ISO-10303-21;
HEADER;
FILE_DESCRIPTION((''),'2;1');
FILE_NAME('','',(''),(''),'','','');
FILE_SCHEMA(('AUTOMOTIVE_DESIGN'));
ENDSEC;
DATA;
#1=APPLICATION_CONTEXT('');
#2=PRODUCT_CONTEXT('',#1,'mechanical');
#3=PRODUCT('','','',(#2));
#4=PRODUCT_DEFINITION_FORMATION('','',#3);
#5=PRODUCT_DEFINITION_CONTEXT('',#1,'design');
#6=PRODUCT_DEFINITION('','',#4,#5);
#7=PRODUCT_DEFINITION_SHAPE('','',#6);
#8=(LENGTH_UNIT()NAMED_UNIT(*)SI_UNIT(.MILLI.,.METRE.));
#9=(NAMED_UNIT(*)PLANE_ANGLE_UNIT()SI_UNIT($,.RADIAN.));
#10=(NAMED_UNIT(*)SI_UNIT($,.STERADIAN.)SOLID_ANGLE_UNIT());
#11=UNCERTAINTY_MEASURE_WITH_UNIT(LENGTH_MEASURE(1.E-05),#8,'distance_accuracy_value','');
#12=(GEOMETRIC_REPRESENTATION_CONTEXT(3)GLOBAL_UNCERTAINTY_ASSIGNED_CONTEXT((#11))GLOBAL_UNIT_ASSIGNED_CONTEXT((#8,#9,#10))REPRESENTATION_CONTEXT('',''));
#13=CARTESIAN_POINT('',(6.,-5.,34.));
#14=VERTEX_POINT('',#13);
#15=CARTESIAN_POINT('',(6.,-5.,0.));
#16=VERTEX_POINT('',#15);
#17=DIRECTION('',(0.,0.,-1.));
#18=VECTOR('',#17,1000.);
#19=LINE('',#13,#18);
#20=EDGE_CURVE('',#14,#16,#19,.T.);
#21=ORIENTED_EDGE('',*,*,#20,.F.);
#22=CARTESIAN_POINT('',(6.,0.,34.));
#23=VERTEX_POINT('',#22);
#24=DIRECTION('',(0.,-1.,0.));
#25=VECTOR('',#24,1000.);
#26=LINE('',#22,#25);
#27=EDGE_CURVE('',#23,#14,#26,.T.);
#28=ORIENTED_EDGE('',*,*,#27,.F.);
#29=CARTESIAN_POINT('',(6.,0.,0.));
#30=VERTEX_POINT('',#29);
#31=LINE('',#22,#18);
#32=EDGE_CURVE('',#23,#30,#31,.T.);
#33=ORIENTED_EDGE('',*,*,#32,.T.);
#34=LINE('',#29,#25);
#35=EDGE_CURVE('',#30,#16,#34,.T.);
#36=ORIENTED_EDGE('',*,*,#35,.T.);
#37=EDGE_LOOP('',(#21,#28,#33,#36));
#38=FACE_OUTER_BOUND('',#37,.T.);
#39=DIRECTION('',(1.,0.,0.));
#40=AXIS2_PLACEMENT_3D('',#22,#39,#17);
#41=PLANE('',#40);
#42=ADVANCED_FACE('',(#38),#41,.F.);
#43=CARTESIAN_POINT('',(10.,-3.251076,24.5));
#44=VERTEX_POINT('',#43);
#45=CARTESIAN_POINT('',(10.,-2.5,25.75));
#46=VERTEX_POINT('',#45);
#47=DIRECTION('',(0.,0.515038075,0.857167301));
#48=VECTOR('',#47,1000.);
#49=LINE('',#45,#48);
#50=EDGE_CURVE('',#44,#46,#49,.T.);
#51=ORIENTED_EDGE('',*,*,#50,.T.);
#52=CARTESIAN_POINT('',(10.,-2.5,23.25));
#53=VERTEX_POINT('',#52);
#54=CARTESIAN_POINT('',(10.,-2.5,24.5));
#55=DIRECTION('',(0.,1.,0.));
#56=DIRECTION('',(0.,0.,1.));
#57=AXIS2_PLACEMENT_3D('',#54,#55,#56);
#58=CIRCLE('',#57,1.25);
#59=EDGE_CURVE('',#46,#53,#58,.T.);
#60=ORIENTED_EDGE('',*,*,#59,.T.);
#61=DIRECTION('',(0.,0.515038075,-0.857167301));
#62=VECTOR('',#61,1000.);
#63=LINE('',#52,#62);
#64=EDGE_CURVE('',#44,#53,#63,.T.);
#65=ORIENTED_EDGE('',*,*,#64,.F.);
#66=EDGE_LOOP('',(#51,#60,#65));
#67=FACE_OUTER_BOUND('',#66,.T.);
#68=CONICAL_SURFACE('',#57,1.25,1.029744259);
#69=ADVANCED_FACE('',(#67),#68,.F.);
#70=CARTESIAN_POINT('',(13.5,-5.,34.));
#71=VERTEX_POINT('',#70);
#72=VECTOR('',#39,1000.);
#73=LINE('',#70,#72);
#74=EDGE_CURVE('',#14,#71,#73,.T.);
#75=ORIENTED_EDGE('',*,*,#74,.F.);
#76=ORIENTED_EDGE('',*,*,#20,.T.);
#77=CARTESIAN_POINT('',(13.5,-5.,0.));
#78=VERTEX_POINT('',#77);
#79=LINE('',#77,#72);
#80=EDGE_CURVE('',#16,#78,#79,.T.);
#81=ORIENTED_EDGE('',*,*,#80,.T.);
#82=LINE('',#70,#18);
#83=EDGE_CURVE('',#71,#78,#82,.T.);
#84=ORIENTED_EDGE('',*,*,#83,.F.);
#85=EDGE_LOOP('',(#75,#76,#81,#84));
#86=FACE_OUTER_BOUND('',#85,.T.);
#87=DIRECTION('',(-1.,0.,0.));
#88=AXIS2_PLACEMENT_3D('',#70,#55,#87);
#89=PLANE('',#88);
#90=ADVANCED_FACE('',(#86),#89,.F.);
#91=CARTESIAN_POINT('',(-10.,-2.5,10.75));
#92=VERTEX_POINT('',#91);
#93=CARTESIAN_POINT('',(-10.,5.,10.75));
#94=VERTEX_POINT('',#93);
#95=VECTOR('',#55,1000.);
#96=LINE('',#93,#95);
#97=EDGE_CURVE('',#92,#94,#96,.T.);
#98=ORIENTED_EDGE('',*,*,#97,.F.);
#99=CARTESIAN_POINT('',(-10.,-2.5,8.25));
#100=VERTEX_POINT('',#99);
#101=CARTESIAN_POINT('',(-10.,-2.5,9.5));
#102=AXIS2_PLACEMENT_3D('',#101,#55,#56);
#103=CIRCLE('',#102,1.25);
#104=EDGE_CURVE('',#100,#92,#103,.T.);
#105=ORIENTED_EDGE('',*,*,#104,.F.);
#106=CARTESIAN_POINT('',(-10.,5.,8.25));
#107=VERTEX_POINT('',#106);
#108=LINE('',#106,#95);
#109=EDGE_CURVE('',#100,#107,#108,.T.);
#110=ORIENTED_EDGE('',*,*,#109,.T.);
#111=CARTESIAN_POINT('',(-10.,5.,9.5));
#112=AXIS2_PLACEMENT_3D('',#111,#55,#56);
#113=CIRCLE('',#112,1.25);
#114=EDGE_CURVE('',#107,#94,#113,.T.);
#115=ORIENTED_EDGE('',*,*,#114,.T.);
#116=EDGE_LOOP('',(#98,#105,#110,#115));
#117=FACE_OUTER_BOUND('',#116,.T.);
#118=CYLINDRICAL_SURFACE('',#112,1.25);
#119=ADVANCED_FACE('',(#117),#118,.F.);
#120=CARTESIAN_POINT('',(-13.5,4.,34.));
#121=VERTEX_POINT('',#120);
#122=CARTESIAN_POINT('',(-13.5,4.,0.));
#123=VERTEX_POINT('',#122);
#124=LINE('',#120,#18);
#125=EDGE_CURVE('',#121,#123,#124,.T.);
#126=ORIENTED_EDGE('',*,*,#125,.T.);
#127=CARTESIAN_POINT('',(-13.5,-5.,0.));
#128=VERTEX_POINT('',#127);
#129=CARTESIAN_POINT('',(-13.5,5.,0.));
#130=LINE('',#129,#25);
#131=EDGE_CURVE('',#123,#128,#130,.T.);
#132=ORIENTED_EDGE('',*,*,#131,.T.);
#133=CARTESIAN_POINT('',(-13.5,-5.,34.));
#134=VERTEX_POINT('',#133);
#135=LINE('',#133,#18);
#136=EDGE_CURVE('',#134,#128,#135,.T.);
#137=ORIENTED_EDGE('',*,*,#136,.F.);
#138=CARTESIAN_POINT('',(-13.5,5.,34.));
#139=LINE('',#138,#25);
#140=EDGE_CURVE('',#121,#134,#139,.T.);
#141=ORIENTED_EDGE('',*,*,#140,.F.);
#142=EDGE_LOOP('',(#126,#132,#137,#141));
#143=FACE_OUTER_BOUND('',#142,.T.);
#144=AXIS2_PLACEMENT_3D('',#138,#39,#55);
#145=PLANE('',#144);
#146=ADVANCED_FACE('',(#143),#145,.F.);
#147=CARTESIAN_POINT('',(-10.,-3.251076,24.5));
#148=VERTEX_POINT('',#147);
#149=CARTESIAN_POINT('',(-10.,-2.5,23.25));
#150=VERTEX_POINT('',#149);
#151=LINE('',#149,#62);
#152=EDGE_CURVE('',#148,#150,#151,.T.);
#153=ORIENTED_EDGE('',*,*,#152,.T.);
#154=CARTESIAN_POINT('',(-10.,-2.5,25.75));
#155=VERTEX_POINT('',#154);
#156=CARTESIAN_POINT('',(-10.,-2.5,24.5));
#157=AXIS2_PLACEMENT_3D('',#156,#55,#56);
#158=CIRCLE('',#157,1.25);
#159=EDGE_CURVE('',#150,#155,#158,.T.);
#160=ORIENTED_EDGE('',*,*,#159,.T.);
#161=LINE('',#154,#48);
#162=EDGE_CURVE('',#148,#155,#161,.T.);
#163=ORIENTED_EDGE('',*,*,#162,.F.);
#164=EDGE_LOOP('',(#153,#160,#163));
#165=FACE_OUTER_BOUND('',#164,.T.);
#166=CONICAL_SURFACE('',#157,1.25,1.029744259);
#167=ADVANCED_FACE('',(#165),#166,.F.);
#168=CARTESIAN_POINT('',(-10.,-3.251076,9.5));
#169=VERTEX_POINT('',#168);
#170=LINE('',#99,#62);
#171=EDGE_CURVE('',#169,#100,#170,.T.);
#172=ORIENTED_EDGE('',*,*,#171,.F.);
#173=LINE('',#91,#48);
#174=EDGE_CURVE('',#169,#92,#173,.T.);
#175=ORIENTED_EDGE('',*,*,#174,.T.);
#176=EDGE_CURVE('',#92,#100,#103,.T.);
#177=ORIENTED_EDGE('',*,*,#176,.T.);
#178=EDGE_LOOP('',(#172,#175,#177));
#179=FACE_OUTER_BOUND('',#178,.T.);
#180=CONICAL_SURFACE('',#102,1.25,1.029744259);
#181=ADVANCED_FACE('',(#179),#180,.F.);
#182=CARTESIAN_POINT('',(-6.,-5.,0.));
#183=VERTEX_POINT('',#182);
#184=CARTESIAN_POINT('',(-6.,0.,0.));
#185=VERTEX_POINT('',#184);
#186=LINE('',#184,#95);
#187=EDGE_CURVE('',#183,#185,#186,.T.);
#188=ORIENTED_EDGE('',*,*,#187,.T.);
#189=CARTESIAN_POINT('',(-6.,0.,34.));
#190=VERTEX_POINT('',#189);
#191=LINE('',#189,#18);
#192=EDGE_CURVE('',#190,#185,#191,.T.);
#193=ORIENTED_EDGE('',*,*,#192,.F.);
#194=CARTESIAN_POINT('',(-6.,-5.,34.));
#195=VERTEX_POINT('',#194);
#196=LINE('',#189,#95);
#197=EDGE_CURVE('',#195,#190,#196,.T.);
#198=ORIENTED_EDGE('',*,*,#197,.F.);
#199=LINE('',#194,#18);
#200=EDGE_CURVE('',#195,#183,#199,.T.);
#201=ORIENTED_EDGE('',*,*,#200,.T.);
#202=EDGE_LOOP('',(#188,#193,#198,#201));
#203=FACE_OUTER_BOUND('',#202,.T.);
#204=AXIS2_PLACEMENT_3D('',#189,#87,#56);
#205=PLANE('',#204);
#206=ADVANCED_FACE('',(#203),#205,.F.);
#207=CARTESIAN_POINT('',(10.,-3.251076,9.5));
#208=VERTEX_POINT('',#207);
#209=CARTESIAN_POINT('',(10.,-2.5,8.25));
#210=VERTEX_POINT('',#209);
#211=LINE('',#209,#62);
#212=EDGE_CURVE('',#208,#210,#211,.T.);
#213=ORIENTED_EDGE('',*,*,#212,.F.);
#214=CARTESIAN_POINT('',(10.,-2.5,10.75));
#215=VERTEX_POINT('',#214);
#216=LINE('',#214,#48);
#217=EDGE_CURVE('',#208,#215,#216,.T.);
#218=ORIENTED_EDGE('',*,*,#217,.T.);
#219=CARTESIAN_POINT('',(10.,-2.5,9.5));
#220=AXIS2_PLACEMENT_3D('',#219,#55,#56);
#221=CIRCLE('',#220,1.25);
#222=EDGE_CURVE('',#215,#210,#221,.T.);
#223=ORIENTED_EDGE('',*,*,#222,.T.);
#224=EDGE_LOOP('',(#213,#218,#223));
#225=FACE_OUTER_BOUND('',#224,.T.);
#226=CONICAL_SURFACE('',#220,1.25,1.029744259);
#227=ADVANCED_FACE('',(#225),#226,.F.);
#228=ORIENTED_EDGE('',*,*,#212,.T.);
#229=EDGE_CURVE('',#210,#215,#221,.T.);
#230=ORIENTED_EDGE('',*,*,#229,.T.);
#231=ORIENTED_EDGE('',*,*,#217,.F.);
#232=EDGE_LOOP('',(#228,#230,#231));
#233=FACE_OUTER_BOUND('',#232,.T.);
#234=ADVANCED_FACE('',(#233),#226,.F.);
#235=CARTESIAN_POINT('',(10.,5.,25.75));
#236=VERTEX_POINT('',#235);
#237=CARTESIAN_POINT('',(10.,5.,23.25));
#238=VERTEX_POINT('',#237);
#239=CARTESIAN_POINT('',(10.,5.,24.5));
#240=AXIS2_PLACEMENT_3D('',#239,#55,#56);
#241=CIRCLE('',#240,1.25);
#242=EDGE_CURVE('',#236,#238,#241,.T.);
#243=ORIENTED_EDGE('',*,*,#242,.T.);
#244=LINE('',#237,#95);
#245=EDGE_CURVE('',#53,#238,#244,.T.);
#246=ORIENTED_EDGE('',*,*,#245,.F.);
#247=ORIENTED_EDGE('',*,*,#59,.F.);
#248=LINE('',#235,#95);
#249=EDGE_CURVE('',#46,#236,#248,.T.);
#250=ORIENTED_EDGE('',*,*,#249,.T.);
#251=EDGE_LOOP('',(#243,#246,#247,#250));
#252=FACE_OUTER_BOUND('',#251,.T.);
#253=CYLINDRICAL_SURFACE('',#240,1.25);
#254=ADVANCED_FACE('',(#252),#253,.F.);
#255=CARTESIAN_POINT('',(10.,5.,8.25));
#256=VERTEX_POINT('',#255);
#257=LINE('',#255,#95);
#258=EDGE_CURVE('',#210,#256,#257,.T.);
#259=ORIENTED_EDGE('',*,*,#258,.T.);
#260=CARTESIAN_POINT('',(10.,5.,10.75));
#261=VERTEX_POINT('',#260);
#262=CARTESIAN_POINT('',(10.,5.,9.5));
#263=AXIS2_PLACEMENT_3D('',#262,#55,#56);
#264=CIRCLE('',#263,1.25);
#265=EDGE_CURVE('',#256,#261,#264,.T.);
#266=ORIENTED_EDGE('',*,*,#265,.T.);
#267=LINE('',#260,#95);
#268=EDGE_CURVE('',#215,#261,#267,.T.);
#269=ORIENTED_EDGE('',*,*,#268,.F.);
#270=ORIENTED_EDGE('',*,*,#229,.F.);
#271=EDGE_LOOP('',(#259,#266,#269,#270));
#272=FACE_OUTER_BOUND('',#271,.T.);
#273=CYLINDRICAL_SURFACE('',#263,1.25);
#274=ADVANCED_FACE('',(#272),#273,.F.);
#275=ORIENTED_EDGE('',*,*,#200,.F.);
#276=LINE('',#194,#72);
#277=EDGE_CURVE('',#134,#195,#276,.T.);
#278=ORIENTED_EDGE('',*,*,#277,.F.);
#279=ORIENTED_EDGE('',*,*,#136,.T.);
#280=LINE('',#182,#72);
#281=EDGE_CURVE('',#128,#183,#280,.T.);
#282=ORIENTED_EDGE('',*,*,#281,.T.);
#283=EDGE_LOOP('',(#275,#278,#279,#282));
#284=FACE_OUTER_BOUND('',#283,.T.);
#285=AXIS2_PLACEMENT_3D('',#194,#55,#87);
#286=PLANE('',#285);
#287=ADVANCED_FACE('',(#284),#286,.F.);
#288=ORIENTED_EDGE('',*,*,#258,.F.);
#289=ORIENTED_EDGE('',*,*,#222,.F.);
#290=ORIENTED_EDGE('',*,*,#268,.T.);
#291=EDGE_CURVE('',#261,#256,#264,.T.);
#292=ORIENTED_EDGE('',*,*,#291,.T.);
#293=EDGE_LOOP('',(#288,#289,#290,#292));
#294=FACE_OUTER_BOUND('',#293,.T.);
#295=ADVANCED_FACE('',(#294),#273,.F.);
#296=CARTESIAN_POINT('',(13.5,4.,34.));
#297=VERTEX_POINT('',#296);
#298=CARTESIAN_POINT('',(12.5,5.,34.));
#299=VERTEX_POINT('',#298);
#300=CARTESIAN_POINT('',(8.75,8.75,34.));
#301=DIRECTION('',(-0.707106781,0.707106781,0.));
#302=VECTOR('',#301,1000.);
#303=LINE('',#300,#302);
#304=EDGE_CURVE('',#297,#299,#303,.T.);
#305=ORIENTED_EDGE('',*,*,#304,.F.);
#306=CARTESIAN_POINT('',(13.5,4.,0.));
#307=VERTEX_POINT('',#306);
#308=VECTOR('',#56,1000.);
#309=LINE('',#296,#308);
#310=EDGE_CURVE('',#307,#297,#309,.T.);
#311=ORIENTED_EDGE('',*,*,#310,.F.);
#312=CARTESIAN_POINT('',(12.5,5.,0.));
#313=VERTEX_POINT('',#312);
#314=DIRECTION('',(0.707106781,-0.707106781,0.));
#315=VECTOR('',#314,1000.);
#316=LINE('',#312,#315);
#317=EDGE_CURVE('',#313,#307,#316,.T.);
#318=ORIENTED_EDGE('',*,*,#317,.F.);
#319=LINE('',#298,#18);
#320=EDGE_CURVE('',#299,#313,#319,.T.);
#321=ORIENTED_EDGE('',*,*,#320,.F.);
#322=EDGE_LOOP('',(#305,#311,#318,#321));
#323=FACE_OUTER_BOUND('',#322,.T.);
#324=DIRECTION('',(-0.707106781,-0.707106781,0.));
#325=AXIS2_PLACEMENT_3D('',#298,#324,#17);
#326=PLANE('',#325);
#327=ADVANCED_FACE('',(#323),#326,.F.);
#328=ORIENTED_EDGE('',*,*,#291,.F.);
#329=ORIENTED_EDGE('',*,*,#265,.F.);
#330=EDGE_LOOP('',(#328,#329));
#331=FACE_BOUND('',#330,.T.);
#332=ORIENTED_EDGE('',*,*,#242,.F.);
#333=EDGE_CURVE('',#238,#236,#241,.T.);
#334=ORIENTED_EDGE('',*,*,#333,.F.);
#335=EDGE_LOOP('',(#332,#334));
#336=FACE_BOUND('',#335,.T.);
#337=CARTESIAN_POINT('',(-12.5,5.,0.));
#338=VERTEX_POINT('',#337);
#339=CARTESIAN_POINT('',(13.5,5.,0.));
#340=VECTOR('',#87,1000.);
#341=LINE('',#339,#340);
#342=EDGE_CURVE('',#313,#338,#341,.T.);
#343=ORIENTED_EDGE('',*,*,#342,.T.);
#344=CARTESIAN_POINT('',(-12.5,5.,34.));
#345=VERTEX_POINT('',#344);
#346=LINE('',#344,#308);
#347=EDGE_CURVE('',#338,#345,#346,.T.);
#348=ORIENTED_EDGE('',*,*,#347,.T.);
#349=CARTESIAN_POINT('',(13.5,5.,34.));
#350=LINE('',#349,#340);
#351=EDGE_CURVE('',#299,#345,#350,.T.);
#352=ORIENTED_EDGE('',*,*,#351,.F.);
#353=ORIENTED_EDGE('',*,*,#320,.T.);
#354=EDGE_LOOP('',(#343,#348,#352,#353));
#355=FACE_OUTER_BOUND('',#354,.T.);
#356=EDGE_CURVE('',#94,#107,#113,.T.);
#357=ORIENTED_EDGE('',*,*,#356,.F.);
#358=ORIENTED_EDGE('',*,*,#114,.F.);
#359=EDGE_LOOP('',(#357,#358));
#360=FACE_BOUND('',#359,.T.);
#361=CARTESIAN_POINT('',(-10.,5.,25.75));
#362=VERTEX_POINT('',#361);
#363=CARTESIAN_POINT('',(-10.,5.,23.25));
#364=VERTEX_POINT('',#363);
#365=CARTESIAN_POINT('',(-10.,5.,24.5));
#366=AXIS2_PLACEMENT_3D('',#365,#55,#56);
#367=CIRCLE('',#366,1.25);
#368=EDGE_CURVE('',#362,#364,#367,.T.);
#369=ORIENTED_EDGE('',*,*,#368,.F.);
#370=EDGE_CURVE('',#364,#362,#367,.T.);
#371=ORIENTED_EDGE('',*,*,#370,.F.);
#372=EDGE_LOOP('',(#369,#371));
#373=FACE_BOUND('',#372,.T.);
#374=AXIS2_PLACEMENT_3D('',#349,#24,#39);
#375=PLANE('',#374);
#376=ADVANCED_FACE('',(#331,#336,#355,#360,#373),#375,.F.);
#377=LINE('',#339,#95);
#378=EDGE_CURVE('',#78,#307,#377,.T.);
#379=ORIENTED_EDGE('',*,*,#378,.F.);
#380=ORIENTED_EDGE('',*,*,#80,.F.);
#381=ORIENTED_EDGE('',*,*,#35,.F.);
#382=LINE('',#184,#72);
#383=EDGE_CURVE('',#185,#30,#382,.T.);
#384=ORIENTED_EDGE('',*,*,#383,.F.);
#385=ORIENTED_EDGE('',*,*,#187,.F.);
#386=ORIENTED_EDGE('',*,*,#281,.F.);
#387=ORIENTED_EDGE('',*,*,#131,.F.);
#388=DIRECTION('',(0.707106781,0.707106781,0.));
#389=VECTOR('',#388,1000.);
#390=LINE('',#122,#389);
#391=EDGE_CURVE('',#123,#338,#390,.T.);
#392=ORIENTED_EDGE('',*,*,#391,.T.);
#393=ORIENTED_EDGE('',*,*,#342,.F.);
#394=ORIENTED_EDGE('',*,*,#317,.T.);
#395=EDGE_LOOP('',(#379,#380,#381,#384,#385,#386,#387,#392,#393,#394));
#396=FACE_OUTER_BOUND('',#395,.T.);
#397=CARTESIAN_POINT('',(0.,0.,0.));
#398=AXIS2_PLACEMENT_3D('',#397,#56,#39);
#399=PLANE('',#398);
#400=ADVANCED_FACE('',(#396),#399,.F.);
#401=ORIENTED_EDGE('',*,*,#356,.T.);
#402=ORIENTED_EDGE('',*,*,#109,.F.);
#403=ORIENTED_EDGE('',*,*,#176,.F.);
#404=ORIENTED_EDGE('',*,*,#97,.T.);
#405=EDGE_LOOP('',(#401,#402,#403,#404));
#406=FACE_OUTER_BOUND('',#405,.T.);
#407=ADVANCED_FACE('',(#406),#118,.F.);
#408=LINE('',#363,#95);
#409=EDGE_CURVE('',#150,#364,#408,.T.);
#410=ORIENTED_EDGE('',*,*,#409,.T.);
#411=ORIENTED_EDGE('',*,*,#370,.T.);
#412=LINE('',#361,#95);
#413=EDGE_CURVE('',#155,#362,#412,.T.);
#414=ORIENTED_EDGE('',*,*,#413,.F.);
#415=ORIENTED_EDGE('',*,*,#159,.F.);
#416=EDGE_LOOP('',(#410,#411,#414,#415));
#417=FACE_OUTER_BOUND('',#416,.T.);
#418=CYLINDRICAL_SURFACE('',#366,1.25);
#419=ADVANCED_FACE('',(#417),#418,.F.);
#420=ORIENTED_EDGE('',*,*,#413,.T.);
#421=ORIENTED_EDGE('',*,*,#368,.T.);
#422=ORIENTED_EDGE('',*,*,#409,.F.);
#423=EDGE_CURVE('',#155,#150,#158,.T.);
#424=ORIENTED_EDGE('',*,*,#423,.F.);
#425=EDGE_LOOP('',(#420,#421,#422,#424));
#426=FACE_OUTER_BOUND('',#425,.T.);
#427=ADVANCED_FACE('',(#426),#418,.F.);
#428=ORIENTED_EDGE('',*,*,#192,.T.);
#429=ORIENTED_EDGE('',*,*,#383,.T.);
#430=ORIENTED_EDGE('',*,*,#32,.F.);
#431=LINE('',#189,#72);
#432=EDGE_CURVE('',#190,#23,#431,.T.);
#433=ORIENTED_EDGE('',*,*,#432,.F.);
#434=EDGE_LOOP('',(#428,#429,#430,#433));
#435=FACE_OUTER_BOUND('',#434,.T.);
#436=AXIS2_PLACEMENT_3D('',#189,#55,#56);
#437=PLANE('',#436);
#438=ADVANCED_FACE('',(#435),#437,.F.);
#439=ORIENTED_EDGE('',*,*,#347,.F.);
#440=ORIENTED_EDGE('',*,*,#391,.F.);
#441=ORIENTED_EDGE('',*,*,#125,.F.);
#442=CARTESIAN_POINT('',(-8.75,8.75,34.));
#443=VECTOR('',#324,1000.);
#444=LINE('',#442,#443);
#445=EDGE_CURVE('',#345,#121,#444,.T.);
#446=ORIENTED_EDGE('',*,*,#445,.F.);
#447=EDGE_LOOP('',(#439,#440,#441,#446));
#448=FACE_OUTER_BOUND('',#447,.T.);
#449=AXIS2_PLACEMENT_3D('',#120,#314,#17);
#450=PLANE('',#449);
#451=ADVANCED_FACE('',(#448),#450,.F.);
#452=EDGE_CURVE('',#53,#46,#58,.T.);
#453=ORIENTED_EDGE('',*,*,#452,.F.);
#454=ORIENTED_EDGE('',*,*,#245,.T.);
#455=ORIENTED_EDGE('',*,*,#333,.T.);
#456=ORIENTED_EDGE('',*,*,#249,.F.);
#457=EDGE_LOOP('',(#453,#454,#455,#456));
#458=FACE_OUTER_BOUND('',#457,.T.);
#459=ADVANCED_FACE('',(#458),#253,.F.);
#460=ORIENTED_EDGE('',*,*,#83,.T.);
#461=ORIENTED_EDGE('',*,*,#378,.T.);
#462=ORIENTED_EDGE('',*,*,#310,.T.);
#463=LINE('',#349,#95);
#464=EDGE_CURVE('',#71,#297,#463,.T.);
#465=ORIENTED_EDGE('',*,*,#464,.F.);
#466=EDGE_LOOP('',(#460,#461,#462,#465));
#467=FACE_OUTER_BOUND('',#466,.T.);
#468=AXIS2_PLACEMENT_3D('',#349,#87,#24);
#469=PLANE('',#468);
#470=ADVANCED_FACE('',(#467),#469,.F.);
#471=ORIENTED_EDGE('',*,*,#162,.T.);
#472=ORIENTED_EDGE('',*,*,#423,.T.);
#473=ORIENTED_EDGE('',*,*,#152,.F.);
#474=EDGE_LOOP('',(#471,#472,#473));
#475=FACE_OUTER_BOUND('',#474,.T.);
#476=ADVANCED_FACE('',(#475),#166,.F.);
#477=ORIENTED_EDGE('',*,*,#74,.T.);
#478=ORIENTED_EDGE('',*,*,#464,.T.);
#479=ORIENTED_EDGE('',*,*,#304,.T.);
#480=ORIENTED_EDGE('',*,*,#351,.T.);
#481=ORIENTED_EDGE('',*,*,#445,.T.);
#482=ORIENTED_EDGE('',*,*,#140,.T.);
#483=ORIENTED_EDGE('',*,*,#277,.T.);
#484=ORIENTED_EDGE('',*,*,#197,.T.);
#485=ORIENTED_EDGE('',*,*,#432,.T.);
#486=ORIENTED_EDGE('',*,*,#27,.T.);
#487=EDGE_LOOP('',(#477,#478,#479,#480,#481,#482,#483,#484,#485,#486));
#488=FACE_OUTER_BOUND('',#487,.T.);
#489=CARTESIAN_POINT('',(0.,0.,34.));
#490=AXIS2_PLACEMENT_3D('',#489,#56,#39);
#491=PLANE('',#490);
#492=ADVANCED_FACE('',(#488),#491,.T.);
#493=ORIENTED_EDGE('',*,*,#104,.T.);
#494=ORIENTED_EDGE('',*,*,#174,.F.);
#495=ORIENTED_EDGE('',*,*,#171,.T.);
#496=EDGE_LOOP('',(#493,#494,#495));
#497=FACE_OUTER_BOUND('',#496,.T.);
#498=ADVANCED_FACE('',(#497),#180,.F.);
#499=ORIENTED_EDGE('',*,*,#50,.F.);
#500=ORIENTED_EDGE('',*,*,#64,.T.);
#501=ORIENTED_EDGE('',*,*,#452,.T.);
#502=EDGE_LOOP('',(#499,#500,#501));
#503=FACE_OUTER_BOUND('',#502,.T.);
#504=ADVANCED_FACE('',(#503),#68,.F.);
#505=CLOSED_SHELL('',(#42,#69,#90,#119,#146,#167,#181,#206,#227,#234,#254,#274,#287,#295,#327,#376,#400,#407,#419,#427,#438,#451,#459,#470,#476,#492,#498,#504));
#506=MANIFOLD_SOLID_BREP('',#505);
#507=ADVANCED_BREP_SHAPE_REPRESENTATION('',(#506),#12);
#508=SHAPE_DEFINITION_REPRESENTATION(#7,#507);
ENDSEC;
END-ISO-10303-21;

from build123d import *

# Parameters (mm, degrees)
EXTRUDE_1_DEPTH        = 34
HOLE_WIZARD_M3_1_D     = 2.5
HOLE_WIZARD_M3_1_DEPTH = 7.5
HOLE_WIZARD_M3_1_TIP   = 0.751075774
CHAMFER_1_SIZE         = 1


with BuildPart() as part:
    # 草图1 → 凸台-拉伸1 (new body)
    with BuildSketch(Plane.XY):
        Polygon((-6, 0), (6, 0), (6, -5), (13.5, -5), (13.5, 5), (-13.5, 5), (-13.5, -5), (-6, -5), align=None)
    extrude(amount=EXTRUDE_1_DEPTH)

    # M3 螺纹孔1
    with Locations(Plane(origin=(0, 5, 0), x_dir=(1, 0, 0), z_dir=(0, 1, 0))):
        with Locations((-10, -9.5), (10, -9.5), (-10, -24.5), (10, -24.5)):
            Hole(HOLE_WIZARD_M3_1_D / 2, depth=HOLE_WIZARD_M3_1_DEPTH)
            with Locations((0, 0, -(HOLE_WIZARD_M3_1_DEPTH + HOLE_WIZARD_M3_1_TIP / 2))):  # 118° drill point
                Cone(0, HOLE_WIZARD_M3_1_D / 2, HOLE_WIZARD_M3_1_TIP, mode=Mode.SUBTRACT)

    # 倒角1
    chamfer_1_edges = [part.edges().sort_by_distance(p)[0] for p in [
        (-13.5, 5, 17),
        (13.5, 5, 17),
    ]]
    chamfer(chamfer_1_edges, length=CHAMFER_1_SIZE)


solid = part.part
